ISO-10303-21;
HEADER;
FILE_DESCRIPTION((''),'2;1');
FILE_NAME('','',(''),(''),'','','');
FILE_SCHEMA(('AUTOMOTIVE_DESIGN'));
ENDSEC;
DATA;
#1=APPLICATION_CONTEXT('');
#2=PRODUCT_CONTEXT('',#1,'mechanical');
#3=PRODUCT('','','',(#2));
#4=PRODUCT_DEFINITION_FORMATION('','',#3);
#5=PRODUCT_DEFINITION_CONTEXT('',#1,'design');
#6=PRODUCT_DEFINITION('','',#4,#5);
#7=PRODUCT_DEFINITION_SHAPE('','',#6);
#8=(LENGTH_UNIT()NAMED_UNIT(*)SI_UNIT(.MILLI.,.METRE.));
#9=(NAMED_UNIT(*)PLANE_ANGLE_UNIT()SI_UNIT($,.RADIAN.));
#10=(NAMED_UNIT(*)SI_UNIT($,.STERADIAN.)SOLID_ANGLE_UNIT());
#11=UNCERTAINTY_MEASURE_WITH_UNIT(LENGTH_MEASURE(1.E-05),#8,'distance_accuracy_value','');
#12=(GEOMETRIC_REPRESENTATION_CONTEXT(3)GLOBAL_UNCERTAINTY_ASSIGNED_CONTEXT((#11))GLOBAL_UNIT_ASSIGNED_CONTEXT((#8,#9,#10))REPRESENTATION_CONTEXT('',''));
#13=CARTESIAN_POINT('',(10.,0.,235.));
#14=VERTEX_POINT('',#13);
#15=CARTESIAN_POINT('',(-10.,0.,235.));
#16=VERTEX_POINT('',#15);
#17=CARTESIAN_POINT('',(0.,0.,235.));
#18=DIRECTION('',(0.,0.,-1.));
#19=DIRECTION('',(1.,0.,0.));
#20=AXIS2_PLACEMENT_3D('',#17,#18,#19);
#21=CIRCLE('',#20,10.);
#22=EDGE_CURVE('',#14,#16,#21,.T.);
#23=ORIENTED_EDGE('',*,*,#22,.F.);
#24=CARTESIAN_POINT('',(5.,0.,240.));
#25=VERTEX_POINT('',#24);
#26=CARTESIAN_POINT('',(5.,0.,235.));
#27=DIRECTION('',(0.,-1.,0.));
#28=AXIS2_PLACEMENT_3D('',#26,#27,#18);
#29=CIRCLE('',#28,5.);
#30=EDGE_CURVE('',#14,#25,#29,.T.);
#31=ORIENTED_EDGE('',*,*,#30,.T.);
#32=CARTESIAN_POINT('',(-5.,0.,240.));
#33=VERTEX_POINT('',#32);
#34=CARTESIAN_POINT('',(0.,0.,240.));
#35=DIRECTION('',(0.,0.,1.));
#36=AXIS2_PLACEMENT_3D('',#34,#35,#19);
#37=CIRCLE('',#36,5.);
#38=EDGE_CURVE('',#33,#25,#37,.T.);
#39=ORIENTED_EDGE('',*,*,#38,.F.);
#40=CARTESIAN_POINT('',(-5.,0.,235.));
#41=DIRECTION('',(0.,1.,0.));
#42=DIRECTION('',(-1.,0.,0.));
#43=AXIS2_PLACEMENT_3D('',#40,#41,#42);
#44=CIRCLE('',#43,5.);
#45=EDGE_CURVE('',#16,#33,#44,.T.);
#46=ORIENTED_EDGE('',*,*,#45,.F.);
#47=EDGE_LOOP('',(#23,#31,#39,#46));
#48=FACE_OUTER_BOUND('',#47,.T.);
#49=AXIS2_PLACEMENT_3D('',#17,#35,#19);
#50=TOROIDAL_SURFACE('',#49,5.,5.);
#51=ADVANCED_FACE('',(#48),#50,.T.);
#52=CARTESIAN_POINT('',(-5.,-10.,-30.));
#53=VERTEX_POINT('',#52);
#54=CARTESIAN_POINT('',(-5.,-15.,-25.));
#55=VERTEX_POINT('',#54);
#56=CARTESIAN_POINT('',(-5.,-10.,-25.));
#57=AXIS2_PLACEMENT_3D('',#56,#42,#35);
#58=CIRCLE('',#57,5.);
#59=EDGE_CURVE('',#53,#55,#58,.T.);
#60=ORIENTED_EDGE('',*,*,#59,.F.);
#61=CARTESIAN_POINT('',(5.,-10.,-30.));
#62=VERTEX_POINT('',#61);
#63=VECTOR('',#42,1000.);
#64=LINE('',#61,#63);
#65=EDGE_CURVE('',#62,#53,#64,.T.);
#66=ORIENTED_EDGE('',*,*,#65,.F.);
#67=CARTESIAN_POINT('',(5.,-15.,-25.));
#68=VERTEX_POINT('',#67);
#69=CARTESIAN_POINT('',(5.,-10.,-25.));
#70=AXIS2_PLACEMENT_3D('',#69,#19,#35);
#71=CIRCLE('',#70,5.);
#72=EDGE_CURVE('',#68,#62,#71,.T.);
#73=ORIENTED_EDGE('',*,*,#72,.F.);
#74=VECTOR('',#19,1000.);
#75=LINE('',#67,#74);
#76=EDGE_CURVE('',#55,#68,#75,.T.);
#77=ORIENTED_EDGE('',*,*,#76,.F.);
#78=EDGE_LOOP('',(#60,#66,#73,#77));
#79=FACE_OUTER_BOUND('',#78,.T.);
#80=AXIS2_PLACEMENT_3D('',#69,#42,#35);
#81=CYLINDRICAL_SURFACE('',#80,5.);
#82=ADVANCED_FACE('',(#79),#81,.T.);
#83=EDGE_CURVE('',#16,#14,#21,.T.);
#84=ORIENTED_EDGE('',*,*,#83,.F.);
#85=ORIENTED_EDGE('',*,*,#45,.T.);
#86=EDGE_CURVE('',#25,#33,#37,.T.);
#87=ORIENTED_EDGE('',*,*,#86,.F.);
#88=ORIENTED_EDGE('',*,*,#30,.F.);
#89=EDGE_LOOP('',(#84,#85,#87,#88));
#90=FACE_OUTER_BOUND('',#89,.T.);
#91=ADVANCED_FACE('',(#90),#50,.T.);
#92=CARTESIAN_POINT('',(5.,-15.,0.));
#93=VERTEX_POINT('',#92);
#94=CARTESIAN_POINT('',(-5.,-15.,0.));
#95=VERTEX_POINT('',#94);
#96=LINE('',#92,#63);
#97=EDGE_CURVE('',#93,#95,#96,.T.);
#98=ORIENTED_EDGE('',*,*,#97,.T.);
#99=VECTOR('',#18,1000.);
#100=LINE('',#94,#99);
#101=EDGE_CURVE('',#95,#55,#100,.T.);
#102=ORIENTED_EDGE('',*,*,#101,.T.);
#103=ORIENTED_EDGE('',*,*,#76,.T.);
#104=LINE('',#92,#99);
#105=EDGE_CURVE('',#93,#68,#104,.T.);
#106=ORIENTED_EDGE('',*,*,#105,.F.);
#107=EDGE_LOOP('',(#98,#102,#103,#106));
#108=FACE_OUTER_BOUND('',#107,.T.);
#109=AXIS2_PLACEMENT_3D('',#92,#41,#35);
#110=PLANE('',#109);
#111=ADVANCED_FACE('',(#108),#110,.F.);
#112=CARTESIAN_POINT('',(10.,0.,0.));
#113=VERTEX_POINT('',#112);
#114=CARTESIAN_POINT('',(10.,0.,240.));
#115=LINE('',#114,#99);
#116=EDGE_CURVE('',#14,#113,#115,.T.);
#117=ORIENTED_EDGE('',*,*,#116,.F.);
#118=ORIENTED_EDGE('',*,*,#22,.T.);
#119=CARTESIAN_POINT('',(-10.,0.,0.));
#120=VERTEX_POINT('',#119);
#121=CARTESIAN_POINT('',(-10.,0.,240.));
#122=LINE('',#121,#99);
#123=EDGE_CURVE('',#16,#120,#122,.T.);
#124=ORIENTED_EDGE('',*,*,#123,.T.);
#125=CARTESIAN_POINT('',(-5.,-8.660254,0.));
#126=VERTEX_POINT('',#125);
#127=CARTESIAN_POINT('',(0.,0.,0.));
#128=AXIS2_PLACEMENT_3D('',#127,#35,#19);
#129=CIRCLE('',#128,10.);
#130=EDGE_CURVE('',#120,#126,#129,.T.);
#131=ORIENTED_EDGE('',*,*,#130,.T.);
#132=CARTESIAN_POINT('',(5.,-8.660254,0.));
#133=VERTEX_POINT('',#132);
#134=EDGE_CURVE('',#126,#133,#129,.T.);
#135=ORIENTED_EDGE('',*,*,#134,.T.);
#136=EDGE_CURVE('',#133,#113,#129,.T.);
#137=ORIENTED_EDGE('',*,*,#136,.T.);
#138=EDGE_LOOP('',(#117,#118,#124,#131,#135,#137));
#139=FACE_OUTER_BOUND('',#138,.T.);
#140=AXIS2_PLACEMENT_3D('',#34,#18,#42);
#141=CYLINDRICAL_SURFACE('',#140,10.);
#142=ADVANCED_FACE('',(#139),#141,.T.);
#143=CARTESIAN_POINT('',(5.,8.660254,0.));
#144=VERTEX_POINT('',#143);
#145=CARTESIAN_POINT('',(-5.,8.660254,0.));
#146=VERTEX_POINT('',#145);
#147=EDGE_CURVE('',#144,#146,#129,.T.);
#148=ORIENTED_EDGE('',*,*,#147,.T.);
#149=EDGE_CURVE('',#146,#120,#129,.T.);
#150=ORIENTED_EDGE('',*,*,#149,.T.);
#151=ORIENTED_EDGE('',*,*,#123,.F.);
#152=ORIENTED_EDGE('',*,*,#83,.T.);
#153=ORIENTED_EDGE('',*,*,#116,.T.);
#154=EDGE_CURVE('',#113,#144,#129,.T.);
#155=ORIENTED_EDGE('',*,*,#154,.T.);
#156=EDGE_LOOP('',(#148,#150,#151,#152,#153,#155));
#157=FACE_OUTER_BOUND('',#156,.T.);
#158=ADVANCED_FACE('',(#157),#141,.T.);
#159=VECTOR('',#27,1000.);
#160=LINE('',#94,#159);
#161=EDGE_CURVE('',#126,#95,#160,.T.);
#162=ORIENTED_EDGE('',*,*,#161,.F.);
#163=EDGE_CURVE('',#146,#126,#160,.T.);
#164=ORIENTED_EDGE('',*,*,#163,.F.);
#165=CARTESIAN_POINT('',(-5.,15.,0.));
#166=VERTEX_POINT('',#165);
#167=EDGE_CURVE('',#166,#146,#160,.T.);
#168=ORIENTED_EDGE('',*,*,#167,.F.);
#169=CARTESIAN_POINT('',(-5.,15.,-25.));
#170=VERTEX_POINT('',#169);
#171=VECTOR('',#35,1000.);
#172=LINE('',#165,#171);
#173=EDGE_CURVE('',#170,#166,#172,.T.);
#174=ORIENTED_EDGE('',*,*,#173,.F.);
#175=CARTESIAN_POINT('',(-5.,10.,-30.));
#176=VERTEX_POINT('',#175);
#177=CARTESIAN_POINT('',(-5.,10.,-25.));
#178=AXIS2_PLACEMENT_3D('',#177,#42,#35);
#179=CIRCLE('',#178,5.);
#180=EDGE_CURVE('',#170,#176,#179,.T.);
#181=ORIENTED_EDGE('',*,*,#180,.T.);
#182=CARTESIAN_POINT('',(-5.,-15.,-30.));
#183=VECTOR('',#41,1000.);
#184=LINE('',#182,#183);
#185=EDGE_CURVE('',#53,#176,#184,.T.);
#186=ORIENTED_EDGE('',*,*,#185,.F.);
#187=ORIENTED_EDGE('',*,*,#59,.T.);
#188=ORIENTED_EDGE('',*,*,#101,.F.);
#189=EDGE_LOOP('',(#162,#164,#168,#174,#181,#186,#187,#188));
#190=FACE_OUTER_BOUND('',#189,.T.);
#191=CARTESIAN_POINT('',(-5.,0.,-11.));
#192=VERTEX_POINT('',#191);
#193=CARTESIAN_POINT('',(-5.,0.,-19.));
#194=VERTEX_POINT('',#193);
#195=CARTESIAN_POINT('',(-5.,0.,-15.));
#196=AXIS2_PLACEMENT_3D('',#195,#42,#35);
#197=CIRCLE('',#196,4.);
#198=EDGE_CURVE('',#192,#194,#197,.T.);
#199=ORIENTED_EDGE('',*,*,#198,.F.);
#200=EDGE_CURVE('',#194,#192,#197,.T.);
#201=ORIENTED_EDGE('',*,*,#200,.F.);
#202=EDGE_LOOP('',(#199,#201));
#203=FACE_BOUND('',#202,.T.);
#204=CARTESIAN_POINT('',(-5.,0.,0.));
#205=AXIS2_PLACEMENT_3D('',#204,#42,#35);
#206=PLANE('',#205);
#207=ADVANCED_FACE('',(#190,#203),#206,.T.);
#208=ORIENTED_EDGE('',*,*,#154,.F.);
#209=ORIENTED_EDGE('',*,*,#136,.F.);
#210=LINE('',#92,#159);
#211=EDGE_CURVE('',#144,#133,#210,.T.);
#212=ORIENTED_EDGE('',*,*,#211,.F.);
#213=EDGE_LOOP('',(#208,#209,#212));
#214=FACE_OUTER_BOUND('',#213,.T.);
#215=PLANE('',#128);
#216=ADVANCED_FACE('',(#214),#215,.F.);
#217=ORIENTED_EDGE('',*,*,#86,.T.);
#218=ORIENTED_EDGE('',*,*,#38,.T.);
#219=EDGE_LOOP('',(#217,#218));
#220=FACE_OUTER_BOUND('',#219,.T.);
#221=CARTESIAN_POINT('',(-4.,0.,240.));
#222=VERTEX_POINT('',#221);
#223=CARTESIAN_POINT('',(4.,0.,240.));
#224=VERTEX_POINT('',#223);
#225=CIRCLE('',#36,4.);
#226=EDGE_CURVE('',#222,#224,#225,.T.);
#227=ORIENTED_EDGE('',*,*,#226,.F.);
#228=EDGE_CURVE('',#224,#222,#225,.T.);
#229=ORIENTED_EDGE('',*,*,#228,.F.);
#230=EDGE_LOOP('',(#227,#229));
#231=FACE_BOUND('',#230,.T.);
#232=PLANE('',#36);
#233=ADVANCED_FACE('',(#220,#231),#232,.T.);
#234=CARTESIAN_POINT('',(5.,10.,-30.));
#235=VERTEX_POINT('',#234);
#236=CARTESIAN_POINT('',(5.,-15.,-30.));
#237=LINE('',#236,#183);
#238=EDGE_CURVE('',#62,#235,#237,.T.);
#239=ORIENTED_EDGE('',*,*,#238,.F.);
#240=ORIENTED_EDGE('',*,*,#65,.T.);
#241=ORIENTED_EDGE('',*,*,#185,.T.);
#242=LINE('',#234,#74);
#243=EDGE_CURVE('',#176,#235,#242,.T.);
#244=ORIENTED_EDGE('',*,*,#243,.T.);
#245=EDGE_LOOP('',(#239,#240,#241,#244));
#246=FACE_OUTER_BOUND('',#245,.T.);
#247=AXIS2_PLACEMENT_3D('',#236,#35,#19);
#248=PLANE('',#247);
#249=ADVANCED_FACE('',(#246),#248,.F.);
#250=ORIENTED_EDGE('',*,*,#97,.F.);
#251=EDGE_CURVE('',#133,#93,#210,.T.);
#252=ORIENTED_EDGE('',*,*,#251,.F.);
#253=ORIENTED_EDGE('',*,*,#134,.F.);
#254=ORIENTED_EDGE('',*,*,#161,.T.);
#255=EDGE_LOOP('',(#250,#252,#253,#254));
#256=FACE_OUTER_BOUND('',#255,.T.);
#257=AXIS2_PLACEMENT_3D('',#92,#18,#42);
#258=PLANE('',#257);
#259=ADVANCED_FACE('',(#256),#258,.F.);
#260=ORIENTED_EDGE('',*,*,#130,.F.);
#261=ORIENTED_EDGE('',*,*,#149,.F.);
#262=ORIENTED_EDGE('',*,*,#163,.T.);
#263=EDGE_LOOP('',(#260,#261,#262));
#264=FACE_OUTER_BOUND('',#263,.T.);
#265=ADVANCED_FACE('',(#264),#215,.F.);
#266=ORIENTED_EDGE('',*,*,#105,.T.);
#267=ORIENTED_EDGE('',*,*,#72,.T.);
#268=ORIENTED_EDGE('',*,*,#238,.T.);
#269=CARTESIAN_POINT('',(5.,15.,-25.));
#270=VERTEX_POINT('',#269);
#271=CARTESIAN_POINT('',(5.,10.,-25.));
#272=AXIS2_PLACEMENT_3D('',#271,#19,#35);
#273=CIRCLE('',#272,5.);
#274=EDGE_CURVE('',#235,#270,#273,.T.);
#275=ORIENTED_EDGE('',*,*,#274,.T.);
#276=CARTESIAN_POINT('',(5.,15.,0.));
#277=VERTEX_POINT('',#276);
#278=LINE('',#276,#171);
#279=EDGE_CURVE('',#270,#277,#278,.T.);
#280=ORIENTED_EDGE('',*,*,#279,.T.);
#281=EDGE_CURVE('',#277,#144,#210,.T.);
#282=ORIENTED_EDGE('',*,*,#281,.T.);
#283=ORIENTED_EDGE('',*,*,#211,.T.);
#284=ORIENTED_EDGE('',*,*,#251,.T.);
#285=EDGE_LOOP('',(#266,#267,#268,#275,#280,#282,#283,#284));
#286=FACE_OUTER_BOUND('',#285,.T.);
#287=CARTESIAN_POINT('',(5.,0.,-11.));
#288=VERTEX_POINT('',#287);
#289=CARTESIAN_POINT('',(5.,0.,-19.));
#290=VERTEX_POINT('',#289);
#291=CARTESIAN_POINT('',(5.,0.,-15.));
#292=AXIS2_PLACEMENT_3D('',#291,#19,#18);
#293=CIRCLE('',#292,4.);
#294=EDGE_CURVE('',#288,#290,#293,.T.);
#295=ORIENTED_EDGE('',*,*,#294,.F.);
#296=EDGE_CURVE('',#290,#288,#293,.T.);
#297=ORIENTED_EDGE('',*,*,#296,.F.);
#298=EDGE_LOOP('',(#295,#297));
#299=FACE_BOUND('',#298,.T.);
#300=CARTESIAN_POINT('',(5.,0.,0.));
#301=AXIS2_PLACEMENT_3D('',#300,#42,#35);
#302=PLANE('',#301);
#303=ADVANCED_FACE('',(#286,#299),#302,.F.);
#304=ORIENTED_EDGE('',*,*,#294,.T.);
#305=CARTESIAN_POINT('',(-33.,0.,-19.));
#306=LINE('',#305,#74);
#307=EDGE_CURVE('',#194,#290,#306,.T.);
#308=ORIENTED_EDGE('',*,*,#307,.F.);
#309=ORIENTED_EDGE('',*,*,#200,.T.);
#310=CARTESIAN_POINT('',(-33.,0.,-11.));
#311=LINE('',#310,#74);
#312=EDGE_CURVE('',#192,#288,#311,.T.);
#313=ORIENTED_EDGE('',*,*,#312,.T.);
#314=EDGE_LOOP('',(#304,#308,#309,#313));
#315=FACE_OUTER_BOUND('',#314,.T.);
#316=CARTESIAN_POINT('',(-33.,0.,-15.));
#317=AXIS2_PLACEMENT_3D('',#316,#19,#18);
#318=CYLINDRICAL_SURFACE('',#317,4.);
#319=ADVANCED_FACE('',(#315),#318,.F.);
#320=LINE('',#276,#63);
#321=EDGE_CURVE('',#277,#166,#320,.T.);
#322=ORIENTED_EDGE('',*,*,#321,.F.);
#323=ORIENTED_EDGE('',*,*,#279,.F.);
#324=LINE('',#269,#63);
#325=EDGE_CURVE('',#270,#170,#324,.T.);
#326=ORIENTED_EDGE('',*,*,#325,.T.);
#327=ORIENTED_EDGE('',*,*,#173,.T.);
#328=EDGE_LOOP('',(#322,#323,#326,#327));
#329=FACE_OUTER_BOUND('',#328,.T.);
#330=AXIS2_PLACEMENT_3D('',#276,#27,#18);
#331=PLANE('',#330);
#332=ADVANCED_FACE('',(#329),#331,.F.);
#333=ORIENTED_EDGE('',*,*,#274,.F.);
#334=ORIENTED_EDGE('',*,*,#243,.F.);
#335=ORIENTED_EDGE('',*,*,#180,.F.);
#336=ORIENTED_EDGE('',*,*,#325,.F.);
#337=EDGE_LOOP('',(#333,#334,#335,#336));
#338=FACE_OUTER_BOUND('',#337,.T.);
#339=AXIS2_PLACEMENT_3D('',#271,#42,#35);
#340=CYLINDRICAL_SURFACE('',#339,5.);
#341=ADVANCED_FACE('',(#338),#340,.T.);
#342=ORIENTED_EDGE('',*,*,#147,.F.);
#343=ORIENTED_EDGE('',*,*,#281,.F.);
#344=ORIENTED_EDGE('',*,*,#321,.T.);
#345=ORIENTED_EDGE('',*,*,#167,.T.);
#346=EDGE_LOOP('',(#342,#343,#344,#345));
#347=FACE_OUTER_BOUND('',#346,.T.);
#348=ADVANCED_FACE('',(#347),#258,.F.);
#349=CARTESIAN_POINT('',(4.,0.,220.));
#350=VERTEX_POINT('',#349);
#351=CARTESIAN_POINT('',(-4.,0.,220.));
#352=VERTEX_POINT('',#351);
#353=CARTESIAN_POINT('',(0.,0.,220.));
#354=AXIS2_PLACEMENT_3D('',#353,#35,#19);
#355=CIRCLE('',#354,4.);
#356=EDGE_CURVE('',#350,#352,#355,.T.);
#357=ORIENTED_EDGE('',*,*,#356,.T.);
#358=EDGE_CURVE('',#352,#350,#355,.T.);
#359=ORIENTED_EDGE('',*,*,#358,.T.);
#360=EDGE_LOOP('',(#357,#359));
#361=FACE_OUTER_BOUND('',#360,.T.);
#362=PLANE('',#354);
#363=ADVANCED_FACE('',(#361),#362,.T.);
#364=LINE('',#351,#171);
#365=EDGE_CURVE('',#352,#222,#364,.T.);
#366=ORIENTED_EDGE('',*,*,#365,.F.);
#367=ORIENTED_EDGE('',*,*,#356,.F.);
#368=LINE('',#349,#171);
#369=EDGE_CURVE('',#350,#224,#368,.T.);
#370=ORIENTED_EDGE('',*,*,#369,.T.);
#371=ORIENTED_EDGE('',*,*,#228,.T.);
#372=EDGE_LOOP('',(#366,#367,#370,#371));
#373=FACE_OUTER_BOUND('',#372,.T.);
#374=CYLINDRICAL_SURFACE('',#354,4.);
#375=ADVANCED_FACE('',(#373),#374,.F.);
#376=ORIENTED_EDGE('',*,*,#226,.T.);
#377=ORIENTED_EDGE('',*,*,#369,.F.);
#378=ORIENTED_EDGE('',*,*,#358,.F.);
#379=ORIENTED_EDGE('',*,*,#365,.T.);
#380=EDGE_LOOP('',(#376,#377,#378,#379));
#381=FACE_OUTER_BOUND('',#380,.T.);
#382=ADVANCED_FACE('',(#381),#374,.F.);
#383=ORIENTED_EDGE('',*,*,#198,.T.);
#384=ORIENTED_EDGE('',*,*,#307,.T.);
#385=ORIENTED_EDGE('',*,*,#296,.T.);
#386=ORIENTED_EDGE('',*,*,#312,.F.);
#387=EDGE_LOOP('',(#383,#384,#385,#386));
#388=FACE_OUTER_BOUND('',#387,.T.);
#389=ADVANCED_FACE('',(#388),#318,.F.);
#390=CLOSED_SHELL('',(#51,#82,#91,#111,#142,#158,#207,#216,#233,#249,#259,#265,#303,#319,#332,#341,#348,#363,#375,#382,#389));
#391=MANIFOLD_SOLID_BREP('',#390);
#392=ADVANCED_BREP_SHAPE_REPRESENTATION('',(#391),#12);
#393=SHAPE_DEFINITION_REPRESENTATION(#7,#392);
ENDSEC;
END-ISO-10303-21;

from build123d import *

# Parameters (mm, degrees)
SKETCH1_R           = 10
BOSS_EXTRUDE1_DEPTH = 240
SKETCH2_W           = 30
SKETCH2_H           = 30
BOSS_EXTRUDE2_DEPTH = 5
SKETCH3_R           = 4
CUT_EXTRUDE1_DEPTH  = 38
FILLET1_R           = 5
FILLET2_R           = 5
SKETCH4_R           = 4
CUT_EXTRUDE2_DEPTH  = 20


with BuildPart() as part:
    # Sketch1 → Boss-Extrude1 (new body)
    with BuildSketch(Plane.XY):
        Circle(SKETCH1_R)
    extrude(amount=BOSS_EXTRUDE1_DEPTH)

    # Sketch2 → Boss-Extrude2 (add, symmetric)
    with BuildSketch(Plane(origin=(0, 0, 0), x_dir=(0, 0, -1), z_dir=(1, 0, 0))):
        with Locations((15, 0)):
            Rectangle(SKETCH2_W, SKETCH2_H)
    extrude(amount=BOSS_EXTRUDE2_DEPTH, both=True)

    # Sketch3 → Cut-Extrude1 (cut)
    with BuildSketch(Plane(origin=(5, 0, 0), x_dir=(0, 0, -1), z_dir=(1, 0, 0))):
        with Locations((15, 0)):
            Circle(SKETCH3_R)
    extrude(amount=-CUT_EXTRUDE1_DEPTH, mode=Mode.SUBTRACT)

    # Fillet1
    fillet1_edges = [part.edges().sort_by_distance(p)[0] for p in [
        (0, -15, -30),
        (0, 15, -30),
    ]]
    fillet(fillet1_edges, radius=FILLET1_R)

    # Fillet2
    fillet2_edges = [part.edges().sort_by_distance(p)[0] for p in [
        (-10, 0, 240),
    ]]
    fillet(fillet2_edges, radius=FILLET2_R)

    # Sketch4 → Cut-Extrude2 (cut)
    with BuildSketch(Plane.XY.offset(240)):
        Circle(SKETCH4_R)
    extrude(amount=-CUT_EXTRUDE2_DEPTH, mode=Mode.SUBTRACT)


solid = part.part
